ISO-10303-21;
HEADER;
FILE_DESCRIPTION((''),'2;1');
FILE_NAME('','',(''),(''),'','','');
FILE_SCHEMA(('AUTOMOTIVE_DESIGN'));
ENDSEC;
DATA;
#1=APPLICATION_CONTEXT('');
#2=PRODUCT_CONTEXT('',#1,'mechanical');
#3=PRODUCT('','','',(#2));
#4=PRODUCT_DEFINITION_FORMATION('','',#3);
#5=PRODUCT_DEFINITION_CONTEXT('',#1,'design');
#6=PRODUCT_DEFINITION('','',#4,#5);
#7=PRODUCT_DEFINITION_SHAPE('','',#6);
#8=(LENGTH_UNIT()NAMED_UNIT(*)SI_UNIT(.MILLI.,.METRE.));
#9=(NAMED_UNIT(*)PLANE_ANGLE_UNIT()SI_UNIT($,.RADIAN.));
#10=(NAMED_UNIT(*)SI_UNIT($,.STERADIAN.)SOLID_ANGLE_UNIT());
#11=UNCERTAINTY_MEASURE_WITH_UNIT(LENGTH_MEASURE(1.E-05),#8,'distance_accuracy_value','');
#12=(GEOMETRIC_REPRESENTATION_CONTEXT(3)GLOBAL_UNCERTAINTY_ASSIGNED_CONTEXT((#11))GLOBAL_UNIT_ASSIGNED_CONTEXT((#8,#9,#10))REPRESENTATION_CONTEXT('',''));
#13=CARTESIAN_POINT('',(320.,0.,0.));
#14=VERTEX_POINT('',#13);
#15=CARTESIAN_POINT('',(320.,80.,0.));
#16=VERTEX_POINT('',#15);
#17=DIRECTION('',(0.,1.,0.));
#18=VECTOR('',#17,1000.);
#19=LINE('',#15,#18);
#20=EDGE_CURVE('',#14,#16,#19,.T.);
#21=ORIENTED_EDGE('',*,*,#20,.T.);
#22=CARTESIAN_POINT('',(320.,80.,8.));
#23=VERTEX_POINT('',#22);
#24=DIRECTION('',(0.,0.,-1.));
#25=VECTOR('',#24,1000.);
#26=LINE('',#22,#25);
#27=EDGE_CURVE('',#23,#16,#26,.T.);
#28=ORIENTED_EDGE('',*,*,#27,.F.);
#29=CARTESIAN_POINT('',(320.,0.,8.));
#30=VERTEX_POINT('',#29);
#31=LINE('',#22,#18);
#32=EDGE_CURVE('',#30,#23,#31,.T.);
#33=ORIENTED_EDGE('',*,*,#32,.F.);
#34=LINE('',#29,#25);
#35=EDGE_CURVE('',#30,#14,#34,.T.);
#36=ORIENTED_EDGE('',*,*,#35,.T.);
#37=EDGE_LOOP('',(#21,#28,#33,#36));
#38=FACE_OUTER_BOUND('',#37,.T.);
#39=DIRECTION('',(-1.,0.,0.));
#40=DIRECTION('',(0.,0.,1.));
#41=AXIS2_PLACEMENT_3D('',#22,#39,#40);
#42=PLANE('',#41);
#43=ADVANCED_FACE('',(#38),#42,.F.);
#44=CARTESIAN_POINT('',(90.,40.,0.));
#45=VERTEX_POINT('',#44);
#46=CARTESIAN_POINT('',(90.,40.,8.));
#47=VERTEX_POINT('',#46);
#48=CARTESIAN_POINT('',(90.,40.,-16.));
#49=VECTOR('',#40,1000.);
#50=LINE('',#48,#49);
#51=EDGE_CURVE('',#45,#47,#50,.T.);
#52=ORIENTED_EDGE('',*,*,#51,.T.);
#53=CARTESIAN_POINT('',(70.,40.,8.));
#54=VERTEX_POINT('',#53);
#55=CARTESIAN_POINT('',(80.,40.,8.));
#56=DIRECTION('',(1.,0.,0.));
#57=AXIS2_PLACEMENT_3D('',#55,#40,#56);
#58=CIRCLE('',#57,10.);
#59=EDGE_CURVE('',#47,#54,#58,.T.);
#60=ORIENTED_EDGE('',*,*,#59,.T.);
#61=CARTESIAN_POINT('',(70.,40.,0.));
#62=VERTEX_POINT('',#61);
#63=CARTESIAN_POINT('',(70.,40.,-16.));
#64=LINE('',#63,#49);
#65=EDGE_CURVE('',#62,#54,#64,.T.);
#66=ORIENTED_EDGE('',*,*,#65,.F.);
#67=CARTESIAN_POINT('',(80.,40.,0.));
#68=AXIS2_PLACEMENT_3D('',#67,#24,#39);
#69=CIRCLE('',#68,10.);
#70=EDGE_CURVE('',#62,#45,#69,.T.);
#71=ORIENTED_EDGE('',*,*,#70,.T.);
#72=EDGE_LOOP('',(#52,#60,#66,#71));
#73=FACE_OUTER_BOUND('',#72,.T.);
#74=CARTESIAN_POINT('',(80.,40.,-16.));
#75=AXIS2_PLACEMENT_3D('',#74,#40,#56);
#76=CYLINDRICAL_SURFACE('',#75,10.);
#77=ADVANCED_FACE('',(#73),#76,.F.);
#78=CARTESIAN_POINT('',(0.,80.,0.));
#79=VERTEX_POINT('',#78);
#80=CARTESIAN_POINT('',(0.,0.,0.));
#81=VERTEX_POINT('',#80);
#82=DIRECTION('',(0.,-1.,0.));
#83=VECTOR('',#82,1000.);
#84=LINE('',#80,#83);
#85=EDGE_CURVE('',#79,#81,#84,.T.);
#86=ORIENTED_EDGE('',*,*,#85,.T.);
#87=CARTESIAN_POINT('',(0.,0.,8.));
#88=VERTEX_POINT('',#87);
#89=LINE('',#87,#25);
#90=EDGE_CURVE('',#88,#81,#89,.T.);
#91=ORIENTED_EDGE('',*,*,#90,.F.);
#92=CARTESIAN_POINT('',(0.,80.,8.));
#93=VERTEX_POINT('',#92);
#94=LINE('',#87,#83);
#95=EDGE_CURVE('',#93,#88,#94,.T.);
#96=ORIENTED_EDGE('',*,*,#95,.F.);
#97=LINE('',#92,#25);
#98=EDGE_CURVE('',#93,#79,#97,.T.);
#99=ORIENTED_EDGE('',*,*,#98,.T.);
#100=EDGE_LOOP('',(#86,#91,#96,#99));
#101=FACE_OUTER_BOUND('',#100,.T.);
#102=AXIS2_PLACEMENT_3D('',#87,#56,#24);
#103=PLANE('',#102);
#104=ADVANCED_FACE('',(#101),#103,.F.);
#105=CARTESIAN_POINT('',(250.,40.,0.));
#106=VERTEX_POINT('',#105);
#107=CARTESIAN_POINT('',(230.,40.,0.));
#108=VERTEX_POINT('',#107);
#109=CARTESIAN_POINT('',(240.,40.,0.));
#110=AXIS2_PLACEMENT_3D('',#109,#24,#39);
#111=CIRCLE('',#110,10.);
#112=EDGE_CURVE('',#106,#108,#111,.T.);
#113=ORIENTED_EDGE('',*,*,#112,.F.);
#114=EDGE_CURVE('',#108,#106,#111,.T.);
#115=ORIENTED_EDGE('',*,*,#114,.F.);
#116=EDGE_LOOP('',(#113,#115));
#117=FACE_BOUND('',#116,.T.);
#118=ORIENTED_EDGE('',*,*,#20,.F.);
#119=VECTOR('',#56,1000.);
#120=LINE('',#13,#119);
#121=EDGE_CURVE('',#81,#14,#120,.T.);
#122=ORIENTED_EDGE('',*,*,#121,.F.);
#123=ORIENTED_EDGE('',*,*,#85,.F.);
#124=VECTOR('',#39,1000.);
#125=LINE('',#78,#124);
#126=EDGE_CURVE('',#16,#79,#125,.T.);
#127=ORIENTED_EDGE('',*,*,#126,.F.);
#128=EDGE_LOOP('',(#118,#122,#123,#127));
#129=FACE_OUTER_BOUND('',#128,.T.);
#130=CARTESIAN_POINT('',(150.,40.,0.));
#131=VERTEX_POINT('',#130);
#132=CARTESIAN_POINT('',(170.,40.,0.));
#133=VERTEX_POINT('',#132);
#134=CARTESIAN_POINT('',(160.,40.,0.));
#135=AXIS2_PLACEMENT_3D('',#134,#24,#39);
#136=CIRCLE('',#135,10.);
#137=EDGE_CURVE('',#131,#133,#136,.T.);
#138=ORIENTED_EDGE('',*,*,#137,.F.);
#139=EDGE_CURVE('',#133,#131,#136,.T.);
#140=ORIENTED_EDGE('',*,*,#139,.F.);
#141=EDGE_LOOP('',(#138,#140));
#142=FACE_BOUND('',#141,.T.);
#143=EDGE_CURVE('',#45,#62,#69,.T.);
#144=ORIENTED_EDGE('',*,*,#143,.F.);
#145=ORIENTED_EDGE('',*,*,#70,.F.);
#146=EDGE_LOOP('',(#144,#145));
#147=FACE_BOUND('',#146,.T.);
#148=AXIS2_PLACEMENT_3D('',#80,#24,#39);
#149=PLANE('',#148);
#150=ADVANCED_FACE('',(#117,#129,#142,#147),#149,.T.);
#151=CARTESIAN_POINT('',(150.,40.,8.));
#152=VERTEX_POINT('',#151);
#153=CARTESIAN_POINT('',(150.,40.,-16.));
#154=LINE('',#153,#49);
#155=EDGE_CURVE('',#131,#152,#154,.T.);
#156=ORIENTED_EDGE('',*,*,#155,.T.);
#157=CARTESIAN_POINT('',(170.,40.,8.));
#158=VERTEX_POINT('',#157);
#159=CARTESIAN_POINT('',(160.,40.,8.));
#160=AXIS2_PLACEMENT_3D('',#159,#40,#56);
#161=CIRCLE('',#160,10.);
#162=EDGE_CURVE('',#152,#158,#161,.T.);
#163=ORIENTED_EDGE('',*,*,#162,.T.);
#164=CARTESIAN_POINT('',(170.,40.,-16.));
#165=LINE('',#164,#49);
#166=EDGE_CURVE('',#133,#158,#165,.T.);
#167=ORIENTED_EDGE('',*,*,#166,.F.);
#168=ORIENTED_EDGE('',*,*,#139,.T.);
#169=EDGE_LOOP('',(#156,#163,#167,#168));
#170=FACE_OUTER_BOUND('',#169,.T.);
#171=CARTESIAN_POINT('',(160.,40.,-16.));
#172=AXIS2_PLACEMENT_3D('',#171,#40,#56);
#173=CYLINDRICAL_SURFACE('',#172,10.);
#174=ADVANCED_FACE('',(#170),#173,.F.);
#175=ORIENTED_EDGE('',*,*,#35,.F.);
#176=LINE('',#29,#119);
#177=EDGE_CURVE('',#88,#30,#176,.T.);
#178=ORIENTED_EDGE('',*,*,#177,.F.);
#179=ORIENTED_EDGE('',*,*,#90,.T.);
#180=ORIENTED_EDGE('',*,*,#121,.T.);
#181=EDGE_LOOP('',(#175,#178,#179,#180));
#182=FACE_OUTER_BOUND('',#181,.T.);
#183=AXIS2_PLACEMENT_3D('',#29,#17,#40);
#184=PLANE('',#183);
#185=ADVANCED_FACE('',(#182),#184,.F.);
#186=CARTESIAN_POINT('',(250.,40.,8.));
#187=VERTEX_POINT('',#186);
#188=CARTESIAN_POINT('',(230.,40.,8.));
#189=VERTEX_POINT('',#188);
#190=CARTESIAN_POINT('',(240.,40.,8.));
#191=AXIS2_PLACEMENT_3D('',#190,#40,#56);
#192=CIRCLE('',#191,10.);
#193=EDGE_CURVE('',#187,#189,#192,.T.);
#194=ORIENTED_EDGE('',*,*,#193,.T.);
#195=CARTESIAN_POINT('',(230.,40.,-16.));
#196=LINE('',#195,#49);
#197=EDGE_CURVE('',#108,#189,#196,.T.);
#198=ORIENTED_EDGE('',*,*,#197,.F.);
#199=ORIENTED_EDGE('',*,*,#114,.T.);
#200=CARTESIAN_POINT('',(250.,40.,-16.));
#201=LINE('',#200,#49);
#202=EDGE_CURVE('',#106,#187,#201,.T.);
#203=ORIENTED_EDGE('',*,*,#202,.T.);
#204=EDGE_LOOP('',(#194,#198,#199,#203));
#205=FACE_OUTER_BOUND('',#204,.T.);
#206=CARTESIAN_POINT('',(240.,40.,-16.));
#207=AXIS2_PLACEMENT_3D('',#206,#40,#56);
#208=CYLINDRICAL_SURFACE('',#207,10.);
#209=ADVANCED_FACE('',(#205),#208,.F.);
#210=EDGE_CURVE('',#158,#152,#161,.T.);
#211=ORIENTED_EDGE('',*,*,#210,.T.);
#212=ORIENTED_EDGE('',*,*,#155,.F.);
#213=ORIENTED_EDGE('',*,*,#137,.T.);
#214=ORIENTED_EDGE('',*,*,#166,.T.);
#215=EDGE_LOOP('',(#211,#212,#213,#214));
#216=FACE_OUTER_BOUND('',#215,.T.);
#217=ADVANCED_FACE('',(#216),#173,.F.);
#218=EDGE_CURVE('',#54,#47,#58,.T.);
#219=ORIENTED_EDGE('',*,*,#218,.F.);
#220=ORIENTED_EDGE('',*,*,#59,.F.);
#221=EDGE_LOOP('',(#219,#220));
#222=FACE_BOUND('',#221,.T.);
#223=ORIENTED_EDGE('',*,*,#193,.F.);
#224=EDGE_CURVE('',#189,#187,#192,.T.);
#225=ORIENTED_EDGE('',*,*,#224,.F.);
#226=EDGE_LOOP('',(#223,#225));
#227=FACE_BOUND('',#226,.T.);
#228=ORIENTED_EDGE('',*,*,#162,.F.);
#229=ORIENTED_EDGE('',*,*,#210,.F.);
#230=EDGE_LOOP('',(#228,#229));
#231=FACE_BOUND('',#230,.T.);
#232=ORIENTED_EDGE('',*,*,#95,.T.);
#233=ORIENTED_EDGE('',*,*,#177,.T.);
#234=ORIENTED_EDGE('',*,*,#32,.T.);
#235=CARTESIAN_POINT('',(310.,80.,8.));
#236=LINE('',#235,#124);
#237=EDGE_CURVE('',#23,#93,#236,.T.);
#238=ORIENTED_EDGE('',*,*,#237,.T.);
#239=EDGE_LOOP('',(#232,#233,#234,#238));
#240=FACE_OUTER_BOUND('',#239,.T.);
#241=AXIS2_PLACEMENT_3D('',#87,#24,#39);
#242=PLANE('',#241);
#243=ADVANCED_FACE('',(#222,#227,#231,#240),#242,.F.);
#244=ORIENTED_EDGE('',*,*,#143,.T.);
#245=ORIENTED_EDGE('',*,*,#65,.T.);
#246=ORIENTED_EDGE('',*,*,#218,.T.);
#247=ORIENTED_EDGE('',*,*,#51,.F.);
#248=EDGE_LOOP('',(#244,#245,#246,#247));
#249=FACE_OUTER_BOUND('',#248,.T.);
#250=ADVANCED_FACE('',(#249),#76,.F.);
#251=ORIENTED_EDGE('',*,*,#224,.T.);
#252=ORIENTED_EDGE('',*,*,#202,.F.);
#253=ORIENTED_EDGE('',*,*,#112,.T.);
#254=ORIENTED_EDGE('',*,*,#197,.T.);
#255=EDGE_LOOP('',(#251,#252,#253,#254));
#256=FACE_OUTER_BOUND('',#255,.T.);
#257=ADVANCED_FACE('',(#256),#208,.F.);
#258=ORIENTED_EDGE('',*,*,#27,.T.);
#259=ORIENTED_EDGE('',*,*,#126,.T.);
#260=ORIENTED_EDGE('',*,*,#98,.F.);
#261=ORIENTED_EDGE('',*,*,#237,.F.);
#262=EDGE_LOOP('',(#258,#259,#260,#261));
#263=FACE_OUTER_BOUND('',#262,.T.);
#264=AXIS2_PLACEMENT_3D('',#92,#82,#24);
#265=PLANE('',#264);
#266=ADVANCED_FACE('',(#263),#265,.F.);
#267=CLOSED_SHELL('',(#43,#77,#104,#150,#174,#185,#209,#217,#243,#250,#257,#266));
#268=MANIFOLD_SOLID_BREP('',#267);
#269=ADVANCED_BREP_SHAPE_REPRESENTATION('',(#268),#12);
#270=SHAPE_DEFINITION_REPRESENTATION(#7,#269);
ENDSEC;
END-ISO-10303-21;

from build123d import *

# Parameters (mm, degrees)
EXTRUDE_1_DEPTH     = 8
SKETCH_2_R          = 10
CUT_EXTRUDE_1_DEPTH = 24


with BuildPart() as part:
    # 草图1 → 凸台-拉伸1 (new body)
    with BuildSketch(Plane.XY):
        Polygon((0, 0), (0, 80), (310, 80), (320, 80), (320, 0), align=None)
    extrude(amount=EXTRUDE_1_DEPTH)

    # 草图2 → 切除-拉伸1 (cut)
    with BuildSketch(Plane.XY.offset(8)):
        with Locations((80, 40)):
            Circle(SKETCH_2_R)
        with Locations((160, 40)):
            Circle(SKETCH_2_R)
        with Locations((240, 40)):
            Circle(SKETCH_2_R)
    extrude(amount=-CUT_EXTRUDE_1_DEPTH, mode=Mode.SUBTRACT)


solid = part.part
